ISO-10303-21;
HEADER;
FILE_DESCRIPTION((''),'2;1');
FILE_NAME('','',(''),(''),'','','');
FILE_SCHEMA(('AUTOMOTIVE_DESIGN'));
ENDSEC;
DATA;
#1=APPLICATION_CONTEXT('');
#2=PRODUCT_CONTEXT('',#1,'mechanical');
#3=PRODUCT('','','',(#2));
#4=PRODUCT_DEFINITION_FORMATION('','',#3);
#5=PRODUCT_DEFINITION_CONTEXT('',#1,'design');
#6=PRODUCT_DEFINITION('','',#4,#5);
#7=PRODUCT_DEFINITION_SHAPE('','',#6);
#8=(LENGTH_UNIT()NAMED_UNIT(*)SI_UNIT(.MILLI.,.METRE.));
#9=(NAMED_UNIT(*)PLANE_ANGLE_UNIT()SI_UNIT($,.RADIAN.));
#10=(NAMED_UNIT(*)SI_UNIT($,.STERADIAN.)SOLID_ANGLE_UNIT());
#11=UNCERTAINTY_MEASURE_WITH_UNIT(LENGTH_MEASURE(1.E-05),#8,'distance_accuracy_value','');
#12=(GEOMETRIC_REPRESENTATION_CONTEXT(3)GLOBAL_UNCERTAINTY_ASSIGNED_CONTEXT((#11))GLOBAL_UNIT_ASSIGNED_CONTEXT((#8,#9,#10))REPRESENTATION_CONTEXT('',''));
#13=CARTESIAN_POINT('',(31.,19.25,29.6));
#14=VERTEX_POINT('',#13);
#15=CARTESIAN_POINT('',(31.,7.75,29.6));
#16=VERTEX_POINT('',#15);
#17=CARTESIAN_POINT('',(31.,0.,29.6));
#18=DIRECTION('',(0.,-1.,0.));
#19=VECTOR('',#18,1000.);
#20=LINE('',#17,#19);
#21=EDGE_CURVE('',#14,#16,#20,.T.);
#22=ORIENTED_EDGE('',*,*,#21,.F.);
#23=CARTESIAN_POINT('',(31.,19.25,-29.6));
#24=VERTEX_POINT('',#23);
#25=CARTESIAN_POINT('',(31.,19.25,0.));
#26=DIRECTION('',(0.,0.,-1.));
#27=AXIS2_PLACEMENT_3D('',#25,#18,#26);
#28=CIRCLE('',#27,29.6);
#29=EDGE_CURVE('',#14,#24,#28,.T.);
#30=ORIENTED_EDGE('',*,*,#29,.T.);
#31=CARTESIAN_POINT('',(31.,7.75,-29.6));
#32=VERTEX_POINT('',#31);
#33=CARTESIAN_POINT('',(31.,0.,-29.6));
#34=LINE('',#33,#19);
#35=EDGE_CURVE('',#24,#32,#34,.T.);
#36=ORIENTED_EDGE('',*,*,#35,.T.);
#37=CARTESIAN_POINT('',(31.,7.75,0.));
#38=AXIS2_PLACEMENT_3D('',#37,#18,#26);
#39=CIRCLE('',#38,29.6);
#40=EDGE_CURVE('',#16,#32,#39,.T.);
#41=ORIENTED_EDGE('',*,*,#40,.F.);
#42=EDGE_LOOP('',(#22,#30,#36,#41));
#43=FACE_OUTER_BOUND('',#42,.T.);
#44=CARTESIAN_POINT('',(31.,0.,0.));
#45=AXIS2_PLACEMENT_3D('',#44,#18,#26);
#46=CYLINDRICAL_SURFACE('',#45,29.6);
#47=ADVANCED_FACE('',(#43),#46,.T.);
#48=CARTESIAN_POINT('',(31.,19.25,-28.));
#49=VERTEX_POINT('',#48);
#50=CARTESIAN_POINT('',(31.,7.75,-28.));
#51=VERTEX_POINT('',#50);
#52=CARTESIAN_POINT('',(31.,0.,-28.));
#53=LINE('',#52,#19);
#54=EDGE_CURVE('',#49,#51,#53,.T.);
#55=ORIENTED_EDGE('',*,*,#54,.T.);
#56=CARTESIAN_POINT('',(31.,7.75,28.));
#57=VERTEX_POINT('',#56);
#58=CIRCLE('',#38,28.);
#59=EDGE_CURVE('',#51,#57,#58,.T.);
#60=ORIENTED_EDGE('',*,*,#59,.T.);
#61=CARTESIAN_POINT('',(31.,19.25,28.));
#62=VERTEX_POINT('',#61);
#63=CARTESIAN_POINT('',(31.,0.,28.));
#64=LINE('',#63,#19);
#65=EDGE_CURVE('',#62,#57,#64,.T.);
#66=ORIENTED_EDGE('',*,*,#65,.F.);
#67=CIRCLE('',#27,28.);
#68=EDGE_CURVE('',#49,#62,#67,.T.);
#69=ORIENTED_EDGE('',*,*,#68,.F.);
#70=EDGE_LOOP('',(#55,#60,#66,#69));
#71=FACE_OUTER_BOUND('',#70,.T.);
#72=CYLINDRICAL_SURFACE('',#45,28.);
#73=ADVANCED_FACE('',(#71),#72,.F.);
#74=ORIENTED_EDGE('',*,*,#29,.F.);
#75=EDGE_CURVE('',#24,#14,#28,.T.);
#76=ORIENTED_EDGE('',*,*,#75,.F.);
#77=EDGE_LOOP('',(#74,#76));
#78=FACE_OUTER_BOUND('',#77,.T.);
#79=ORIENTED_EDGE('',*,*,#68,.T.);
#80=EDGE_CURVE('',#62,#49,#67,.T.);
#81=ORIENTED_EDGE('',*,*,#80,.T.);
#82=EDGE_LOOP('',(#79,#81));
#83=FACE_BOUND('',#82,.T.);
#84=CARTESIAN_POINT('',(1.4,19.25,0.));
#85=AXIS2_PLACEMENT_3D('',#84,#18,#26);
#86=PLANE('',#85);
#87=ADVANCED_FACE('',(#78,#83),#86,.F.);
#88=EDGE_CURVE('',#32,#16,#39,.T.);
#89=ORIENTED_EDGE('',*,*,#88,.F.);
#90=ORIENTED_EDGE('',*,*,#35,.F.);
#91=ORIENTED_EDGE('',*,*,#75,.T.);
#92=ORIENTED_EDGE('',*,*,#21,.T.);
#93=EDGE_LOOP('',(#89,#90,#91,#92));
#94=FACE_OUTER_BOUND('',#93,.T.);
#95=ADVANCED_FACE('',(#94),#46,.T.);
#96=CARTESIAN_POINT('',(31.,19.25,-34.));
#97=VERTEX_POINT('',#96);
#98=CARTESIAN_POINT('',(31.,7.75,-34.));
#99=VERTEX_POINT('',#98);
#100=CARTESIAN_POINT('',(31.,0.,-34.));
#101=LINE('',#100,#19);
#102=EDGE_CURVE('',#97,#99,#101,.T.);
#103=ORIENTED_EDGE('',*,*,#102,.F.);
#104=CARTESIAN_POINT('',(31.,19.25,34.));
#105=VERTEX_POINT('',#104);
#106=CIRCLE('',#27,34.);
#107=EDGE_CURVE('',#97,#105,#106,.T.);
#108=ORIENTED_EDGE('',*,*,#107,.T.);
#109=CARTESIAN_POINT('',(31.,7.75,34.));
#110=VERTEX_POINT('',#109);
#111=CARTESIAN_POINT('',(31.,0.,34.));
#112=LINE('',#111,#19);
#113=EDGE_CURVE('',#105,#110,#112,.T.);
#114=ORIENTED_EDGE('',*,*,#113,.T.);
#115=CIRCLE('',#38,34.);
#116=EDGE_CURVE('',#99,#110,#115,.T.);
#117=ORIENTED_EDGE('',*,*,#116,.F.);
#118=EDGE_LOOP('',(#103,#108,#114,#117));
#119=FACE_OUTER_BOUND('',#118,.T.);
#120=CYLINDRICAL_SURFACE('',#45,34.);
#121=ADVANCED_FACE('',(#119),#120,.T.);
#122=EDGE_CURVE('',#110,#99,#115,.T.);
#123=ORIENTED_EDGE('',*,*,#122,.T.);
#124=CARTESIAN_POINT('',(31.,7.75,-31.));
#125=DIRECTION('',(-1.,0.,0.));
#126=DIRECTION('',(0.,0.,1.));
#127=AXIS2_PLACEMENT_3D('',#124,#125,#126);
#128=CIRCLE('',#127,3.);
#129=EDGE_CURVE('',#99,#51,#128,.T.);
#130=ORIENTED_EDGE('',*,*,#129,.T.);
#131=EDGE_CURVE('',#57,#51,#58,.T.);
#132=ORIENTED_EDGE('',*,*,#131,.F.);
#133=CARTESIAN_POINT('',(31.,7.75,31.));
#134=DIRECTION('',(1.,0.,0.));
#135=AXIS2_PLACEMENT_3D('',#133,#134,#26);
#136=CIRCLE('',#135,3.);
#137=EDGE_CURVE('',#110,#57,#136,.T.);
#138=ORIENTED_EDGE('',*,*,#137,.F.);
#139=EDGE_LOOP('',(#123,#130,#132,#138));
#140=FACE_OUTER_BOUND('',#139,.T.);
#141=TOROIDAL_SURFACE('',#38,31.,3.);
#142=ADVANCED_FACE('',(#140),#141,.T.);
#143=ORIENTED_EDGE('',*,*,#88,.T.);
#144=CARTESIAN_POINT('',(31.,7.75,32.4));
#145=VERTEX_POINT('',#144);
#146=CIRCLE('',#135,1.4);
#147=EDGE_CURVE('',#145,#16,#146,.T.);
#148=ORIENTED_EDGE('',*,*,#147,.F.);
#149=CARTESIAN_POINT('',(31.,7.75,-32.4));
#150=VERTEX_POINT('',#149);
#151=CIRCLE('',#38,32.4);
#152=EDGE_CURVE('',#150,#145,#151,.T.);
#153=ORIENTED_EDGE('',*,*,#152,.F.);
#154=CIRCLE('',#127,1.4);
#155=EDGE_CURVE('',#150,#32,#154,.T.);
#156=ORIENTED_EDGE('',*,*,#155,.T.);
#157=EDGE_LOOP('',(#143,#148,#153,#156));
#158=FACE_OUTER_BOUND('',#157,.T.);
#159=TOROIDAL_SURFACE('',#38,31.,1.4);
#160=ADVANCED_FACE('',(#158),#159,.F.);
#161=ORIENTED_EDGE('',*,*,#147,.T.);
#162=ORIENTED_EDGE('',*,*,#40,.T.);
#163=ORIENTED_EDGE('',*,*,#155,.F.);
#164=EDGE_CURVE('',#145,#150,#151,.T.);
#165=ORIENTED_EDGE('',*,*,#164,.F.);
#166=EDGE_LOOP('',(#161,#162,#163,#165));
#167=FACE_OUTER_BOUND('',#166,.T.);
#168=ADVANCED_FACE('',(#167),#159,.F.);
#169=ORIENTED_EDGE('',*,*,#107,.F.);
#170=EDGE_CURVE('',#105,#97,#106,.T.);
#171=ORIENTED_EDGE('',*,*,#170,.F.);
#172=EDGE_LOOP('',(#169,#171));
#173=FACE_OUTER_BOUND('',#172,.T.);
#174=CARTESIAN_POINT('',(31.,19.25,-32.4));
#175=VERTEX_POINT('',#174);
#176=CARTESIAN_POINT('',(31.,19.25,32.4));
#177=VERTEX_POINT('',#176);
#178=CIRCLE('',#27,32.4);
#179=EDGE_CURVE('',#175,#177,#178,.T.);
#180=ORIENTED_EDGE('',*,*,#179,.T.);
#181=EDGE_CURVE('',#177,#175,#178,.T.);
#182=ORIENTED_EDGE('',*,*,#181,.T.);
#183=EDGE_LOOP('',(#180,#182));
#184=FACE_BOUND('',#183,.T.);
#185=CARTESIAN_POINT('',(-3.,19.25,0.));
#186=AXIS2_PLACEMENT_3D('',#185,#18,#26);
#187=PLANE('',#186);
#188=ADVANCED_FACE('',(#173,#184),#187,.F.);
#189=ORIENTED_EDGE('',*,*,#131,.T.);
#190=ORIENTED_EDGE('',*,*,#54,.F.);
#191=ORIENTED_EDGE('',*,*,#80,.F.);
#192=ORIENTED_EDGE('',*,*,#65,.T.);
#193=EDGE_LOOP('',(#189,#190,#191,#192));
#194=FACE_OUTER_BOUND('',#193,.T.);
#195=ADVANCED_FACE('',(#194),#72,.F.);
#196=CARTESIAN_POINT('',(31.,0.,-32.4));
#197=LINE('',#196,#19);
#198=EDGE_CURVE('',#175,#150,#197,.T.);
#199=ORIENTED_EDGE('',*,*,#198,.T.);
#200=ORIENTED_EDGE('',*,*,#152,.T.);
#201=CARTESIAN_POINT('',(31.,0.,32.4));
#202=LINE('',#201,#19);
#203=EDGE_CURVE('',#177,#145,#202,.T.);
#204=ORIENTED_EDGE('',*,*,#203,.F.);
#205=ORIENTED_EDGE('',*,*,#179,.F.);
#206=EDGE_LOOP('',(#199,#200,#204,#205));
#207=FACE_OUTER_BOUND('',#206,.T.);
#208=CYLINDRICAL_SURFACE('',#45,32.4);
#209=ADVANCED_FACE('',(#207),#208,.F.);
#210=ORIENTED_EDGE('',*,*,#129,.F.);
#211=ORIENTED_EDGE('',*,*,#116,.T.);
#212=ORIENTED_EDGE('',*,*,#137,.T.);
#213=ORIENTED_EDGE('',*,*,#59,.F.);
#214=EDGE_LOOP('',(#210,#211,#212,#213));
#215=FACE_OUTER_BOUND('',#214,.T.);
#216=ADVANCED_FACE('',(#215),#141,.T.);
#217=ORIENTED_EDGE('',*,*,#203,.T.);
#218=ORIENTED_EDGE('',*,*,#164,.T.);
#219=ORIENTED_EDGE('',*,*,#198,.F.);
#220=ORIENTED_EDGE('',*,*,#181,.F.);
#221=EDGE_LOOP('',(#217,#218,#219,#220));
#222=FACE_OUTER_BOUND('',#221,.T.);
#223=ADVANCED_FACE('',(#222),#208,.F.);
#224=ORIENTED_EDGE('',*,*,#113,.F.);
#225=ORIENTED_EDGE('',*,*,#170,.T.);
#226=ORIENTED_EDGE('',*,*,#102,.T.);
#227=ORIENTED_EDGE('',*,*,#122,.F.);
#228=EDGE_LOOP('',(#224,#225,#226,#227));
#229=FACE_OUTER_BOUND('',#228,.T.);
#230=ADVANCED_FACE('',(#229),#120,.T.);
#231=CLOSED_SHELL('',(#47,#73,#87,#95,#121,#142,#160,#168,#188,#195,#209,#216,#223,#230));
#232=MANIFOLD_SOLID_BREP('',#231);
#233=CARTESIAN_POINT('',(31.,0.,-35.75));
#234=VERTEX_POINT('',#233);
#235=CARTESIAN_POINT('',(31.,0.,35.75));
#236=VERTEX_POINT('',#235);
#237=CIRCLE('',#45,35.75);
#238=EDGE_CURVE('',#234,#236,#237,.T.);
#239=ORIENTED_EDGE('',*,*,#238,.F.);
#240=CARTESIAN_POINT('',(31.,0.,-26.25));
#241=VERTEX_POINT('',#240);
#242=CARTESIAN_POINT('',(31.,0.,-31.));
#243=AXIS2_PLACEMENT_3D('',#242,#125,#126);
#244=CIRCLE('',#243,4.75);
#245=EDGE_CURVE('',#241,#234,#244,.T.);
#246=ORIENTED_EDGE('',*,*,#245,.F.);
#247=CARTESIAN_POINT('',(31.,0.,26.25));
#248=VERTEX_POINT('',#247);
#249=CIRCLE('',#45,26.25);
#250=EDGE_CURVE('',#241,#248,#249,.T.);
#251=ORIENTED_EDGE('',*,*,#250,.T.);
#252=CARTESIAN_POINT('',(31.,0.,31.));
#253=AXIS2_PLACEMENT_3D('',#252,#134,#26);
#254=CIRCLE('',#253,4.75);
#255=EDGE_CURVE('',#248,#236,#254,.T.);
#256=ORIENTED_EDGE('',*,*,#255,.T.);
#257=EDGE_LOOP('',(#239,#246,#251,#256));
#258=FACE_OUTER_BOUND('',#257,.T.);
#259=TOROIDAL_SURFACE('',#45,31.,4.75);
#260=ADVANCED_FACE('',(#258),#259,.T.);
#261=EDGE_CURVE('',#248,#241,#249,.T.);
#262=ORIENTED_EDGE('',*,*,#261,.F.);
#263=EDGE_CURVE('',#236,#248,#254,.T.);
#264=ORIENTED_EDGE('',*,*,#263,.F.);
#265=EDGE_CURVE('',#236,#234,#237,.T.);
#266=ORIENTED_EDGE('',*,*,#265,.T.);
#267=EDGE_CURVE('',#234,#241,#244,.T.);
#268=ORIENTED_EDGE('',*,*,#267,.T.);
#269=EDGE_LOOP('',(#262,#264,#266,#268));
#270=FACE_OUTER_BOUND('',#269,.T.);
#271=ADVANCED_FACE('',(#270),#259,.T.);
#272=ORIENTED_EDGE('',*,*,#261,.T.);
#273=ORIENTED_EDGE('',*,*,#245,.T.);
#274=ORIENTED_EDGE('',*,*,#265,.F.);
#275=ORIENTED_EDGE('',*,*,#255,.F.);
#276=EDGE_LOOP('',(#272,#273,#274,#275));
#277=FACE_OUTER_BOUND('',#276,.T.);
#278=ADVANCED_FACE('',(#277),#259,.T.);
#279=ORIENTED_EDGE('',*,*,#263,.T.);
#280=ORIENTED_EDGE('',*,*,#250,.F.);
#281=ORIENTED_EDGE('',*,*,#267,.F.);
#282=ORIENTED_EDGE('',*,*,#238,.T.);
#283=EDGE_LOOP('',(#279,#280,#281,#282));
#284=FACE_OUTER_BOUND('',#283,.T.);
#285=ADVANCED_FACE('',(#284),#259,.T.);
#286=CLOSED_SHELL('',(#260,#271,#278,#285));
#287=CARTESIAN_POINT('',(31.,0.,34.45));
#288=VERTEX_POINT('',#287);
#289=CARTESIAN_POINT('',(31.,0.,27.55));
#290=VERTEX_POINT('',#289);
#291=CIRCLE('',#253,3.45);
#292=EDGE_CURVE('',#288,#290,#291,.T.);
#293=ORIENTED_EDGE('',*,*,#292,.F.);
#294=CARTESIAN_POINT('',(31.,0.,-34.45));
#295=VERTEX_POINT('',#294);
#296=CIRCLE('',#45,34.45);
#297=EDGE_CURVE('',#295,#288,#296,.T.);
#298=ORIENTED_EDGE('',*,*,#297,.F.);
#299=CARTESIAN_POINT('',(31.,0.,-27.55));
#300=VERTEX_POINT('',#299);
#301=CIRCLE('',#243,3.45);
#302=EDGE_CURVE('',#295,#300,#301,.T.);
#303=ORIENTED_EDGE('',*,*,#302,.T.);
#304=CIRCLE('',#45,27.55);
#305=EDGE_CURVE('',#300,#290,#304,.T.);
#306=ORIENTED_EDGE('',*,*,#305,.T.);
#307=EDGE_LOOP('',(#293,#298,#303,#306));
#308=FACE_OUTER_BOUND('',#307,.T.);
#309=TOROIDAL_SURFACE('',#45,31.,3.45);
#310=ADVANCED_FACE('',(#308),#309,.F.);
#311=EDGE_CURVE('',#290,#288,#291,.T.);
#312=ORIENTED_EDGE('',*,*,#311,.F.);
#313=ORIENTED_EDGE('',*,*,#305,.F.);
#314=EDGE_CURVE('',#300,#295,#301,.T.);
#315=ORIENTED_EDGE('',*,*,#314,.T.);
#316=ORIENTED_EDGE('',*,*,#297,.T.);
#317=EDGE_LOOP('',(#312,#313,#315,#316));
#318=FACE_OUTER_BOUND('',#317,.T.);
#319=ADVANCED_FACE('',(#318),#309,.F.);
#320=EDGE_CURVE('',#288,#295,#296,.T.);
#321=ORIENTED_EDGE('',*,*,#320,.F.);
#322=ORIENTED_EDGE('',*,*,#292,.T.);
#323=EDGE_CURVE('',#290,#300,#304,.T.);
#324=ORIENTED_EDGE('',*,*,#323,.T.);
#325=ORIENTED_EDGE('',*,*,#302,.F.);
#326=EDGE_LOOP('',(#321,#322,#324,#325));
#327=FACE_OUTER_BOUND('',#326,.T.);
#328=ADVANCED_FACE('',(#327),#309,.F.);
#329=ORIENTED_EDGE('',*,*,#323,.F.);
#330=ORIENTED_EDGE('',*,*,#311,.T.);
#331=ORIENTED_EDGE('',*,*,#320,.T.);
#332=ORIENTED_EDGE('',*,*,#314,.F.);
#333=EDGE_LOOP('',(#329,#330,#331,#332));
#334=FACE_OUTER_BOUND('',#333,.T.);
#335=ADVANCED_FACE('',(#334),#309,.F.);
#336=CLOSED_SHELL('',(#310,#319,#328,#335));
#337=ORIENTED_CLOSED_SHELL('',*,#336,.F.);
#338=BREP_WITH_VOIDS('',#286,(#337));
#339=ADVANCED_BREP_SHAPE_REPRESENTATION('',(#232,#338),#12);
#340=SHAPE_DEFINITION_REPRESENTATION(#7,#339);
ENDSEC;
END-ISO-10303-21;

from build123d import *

# Parameters (mm, degrees)
SKETCH3_R   = 4.75
SKETCH3_R_2 = 3.45


with BuildPart() as part:
    # Sweep1: sweep along a path in Sketch 2_2
    with BuildLine(Plane(origin=(0, 0, 0), x_dir=(1, 0, 0), z_dir=(0, 1, 0))) as sweep1_path:
        CenterArc((31, 0), 31, 0, 360)
    # Sketch1 → Sweep1 (sweep)
    with BuildSketch(Plane.XY):
        with BuildLine():
            Line((-3, 19.25), (-3, 7.75))
            ThreePointArc((-3, 7.75), (0, 4.75), (3, 7.75))
            Line((3, 7.75), (3, 19.25))
            Line((3, 19.25), (1.4, 19.25))
            Line((1.4, 19.25), (1.4, 7.75))
            ThreePointArc((1.4, 7.75), (0, 6.35), (-1.4, 7.75))
            Line((-1.4, 7.75), (-1.4, 19.25))
            Line((-1.4, 19.25), (-3, 19.25))
        make_face()
    sweep(path=sweep1_path.line)


with BuildPart() as body_2:
    # Sweep2: sweep along a path in Sketch 2_2 2
    with BuildLine(Plane(origin=(0, 0, 0), x_dir=(1, 0, 0), z_dir=(0, 1, 0))) as sweep2_path:
        CenterArc((31, 0), 31, 0, 360)
    # Sketch3 → Sweep2 (sweep)
    with BuildSketch(Plane.XY):
        Circle(SKETCH3_R)
        Circle(SKETCH3_R_2, mode=Mode.SUBTRACT)
    sweep(path=sweep2_path.line)


solid = Compound([part.part, body_2.part])
